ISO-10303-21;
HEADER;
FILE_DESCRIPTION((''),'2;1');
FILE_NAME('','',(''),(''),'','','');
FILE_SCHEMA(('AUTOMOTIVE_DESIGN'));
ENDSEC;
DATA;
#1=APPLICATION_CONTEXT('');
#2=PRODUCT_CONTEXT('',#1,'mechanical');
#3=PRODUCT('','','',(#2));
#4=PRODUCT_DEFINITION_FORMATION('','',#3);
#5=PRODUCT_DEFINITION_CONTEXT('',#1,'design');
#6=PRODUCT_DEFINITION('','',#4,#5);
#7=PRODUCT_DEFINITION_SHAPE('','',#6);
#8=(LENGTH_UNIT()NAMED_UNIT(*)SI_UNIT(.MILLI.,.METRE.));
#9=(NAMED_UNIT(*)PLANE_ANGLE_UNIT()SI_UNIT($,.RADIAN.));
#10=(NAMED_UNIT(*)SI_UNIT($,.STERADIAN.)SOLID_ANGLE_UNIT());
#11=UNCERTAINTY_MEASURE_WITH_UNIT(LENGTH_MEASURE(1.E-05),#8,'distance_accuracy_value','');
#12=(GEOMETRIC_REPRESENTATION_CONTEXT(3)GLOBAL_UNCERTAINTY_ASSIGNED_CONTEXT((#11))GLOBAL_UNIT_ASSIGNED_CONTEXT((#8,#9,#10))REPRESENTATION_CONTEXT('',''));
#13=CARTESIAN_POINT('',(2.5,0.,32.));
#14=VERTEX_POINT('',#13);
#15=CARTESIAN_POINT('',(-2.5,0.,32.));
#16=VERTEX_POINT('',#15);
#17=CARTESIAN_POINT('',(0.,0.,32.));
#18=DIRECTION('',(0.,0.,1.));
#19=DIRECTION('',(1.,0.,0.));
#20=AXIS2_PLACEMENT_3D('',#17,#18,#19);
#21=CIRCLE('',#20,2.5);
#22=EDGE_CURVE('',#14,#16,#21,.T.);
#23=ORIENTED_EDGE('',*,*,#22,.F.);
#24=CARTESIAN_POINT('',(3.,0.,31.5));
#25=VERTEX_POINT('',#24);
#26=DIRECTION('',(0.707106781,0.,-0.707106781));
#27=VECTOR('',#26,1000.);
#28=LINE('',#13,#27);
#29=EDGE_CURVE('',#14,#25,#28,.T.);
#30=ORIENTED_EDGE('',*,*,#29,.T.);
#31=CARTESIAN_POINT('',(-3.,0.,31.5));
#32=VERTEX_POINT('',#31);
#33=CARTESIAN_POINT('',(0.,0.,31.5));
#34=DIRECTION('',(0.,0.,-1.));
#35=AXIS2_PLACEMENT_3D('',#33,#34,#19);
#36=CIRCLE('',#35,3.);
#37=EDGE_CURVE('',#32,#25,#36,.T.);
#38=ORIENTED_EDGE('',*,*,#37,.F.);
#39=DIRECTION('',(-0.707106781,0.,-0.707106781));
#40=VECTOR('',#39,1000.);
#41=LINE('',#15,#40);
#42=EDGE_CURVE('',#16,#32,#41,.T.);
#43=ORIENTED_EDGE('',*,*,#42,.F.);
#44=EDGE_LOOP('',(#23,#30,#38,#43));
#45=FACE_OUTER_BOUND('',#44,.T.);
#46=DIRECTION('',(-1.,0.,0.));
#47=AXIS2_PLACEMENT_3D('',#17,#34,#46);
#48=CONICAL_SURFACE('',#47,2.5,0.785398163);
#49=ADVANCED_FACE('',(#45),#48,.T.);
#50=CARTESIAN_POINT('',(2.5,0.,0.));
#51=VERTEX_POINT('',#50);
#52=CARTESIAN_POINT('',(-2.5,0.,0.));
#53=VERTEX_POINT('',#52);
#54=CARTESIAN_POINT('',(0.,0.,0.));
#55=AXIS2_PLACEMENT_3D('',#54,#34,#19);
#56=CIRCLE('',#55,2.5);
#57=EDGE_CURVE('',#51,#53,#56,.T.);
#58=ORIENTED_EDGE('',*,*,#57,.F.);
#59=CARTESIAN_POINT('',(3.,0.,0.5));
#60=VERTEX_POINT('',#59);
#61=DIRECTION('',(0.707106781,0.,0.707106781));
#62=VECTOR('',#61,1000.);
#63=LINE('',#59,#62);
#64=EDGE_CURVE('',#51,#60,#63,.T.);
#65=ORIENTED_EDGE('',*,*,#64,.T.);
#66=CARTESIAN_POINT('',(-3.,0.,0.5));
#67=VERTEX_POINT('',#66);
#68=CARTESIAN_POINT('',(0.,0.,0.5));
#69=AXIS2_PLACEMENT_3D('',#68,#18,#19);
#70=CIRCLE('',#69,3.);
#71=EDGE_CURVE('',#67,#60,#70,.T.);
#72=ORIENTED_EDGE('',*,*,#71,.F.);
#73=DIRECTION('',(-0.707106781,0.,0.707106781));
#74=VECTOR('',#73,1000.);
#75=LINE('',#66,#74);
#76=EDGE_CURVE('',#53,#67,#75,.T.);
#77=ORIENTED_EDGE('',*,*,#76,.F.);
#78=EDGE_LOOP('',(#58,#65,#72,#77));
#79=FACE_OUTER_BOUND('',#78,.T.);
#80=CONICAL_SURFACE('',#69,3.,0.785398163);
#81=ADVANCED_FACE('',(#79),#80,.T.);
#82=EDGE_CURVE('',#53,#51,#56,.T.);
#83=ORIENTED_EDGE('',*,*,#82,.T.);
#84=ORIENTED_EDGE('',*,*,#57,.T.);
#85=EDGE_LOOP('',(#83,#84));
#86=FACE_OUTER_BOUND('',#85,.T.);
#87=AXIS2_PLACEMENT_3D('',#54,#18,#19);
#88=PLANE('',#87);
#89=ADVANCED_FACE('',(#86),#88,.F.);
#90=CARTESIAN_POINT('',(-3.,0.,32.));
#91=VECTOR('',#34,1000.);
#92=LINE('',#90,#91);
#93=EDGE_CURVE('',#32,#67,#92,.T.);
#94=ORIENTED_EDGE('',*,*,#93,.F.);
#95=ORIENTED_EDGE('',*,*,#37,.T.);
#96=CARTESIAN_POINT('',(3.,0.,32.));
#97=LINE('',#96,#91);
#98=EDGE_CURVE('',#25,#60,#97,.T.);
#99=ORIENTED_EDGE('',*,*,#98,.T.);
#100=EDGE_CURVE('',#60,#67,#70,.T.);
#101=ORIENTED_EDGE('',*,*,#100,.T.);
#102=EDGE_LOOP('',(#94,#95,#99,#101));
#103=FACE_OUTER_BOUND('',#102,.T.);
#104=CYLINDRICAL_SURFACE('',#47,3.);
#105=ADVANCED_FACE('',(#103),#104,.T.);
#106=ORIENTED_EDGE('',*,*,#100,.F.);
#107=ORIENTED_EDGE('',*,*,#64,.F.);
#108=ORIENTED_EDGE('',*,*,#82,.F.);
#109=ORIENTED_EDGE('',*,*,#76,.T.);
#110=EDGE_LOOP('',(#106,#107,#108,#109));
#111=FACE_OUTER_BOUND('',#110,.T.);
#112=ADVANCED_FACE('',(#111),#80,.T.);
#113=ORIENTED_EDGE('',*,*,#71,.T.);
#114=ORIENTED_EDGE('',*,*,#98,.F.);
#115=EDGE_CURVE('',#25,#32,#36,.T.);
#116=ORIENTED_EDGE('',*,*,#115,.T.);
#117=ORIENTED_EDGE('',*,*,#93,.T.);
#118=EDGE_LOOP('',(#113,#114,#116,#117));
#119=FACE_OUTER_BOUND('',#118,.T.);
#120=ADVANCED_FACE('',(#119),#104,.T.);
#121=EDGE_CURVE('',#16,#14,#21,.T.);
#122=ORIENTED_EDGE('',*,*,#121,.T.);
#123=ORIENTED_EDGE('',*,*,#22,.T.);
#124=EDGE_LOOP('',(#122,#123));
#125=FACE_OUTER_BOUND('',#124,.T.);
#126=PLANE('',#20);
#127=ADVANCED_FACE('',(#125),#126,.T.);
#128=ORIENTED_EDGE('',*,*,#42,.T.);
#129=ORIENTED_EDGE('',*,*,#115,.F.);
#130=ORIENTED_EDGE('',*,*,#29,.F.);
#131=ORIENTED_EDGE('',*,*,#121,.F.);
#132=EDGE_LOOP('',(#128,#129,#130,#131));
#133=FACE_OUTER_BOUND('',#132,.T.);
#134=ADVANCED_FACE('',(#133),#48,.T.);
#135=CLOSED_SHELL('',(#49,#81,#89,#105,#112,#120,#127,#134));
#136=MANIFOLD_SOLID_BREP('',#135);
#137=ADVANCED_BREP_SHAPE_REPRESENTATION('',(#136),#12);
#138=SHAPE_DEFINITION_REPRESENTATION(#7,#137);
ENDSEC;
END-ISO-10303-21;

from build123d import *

# Parameters (mm, degrees)
SKETCH_1_R      = 3
EXTRUDE_1_DEPTH = 32
CHAMFER_1_SIZE  = 0.5


with BuildPart() as part:
    # 草图1 → 凸台-拉伸1 (new body)
    with BuildSketch(Plane.XY):
        Circle(SKETCH_1_R)
    extrude(amount=EXTRUDE_1_DEPTH)

    # 倒角1
    chamfer_1_edges = [part.edges().sort_by_distance(p)[0] for p in [
        (-3, 0, 0),
        (-3, 0, 32),
    ]]
    chamfer(chamfer_1_edges, length=CHAMFER_1_SIZE)


solid = part.part
